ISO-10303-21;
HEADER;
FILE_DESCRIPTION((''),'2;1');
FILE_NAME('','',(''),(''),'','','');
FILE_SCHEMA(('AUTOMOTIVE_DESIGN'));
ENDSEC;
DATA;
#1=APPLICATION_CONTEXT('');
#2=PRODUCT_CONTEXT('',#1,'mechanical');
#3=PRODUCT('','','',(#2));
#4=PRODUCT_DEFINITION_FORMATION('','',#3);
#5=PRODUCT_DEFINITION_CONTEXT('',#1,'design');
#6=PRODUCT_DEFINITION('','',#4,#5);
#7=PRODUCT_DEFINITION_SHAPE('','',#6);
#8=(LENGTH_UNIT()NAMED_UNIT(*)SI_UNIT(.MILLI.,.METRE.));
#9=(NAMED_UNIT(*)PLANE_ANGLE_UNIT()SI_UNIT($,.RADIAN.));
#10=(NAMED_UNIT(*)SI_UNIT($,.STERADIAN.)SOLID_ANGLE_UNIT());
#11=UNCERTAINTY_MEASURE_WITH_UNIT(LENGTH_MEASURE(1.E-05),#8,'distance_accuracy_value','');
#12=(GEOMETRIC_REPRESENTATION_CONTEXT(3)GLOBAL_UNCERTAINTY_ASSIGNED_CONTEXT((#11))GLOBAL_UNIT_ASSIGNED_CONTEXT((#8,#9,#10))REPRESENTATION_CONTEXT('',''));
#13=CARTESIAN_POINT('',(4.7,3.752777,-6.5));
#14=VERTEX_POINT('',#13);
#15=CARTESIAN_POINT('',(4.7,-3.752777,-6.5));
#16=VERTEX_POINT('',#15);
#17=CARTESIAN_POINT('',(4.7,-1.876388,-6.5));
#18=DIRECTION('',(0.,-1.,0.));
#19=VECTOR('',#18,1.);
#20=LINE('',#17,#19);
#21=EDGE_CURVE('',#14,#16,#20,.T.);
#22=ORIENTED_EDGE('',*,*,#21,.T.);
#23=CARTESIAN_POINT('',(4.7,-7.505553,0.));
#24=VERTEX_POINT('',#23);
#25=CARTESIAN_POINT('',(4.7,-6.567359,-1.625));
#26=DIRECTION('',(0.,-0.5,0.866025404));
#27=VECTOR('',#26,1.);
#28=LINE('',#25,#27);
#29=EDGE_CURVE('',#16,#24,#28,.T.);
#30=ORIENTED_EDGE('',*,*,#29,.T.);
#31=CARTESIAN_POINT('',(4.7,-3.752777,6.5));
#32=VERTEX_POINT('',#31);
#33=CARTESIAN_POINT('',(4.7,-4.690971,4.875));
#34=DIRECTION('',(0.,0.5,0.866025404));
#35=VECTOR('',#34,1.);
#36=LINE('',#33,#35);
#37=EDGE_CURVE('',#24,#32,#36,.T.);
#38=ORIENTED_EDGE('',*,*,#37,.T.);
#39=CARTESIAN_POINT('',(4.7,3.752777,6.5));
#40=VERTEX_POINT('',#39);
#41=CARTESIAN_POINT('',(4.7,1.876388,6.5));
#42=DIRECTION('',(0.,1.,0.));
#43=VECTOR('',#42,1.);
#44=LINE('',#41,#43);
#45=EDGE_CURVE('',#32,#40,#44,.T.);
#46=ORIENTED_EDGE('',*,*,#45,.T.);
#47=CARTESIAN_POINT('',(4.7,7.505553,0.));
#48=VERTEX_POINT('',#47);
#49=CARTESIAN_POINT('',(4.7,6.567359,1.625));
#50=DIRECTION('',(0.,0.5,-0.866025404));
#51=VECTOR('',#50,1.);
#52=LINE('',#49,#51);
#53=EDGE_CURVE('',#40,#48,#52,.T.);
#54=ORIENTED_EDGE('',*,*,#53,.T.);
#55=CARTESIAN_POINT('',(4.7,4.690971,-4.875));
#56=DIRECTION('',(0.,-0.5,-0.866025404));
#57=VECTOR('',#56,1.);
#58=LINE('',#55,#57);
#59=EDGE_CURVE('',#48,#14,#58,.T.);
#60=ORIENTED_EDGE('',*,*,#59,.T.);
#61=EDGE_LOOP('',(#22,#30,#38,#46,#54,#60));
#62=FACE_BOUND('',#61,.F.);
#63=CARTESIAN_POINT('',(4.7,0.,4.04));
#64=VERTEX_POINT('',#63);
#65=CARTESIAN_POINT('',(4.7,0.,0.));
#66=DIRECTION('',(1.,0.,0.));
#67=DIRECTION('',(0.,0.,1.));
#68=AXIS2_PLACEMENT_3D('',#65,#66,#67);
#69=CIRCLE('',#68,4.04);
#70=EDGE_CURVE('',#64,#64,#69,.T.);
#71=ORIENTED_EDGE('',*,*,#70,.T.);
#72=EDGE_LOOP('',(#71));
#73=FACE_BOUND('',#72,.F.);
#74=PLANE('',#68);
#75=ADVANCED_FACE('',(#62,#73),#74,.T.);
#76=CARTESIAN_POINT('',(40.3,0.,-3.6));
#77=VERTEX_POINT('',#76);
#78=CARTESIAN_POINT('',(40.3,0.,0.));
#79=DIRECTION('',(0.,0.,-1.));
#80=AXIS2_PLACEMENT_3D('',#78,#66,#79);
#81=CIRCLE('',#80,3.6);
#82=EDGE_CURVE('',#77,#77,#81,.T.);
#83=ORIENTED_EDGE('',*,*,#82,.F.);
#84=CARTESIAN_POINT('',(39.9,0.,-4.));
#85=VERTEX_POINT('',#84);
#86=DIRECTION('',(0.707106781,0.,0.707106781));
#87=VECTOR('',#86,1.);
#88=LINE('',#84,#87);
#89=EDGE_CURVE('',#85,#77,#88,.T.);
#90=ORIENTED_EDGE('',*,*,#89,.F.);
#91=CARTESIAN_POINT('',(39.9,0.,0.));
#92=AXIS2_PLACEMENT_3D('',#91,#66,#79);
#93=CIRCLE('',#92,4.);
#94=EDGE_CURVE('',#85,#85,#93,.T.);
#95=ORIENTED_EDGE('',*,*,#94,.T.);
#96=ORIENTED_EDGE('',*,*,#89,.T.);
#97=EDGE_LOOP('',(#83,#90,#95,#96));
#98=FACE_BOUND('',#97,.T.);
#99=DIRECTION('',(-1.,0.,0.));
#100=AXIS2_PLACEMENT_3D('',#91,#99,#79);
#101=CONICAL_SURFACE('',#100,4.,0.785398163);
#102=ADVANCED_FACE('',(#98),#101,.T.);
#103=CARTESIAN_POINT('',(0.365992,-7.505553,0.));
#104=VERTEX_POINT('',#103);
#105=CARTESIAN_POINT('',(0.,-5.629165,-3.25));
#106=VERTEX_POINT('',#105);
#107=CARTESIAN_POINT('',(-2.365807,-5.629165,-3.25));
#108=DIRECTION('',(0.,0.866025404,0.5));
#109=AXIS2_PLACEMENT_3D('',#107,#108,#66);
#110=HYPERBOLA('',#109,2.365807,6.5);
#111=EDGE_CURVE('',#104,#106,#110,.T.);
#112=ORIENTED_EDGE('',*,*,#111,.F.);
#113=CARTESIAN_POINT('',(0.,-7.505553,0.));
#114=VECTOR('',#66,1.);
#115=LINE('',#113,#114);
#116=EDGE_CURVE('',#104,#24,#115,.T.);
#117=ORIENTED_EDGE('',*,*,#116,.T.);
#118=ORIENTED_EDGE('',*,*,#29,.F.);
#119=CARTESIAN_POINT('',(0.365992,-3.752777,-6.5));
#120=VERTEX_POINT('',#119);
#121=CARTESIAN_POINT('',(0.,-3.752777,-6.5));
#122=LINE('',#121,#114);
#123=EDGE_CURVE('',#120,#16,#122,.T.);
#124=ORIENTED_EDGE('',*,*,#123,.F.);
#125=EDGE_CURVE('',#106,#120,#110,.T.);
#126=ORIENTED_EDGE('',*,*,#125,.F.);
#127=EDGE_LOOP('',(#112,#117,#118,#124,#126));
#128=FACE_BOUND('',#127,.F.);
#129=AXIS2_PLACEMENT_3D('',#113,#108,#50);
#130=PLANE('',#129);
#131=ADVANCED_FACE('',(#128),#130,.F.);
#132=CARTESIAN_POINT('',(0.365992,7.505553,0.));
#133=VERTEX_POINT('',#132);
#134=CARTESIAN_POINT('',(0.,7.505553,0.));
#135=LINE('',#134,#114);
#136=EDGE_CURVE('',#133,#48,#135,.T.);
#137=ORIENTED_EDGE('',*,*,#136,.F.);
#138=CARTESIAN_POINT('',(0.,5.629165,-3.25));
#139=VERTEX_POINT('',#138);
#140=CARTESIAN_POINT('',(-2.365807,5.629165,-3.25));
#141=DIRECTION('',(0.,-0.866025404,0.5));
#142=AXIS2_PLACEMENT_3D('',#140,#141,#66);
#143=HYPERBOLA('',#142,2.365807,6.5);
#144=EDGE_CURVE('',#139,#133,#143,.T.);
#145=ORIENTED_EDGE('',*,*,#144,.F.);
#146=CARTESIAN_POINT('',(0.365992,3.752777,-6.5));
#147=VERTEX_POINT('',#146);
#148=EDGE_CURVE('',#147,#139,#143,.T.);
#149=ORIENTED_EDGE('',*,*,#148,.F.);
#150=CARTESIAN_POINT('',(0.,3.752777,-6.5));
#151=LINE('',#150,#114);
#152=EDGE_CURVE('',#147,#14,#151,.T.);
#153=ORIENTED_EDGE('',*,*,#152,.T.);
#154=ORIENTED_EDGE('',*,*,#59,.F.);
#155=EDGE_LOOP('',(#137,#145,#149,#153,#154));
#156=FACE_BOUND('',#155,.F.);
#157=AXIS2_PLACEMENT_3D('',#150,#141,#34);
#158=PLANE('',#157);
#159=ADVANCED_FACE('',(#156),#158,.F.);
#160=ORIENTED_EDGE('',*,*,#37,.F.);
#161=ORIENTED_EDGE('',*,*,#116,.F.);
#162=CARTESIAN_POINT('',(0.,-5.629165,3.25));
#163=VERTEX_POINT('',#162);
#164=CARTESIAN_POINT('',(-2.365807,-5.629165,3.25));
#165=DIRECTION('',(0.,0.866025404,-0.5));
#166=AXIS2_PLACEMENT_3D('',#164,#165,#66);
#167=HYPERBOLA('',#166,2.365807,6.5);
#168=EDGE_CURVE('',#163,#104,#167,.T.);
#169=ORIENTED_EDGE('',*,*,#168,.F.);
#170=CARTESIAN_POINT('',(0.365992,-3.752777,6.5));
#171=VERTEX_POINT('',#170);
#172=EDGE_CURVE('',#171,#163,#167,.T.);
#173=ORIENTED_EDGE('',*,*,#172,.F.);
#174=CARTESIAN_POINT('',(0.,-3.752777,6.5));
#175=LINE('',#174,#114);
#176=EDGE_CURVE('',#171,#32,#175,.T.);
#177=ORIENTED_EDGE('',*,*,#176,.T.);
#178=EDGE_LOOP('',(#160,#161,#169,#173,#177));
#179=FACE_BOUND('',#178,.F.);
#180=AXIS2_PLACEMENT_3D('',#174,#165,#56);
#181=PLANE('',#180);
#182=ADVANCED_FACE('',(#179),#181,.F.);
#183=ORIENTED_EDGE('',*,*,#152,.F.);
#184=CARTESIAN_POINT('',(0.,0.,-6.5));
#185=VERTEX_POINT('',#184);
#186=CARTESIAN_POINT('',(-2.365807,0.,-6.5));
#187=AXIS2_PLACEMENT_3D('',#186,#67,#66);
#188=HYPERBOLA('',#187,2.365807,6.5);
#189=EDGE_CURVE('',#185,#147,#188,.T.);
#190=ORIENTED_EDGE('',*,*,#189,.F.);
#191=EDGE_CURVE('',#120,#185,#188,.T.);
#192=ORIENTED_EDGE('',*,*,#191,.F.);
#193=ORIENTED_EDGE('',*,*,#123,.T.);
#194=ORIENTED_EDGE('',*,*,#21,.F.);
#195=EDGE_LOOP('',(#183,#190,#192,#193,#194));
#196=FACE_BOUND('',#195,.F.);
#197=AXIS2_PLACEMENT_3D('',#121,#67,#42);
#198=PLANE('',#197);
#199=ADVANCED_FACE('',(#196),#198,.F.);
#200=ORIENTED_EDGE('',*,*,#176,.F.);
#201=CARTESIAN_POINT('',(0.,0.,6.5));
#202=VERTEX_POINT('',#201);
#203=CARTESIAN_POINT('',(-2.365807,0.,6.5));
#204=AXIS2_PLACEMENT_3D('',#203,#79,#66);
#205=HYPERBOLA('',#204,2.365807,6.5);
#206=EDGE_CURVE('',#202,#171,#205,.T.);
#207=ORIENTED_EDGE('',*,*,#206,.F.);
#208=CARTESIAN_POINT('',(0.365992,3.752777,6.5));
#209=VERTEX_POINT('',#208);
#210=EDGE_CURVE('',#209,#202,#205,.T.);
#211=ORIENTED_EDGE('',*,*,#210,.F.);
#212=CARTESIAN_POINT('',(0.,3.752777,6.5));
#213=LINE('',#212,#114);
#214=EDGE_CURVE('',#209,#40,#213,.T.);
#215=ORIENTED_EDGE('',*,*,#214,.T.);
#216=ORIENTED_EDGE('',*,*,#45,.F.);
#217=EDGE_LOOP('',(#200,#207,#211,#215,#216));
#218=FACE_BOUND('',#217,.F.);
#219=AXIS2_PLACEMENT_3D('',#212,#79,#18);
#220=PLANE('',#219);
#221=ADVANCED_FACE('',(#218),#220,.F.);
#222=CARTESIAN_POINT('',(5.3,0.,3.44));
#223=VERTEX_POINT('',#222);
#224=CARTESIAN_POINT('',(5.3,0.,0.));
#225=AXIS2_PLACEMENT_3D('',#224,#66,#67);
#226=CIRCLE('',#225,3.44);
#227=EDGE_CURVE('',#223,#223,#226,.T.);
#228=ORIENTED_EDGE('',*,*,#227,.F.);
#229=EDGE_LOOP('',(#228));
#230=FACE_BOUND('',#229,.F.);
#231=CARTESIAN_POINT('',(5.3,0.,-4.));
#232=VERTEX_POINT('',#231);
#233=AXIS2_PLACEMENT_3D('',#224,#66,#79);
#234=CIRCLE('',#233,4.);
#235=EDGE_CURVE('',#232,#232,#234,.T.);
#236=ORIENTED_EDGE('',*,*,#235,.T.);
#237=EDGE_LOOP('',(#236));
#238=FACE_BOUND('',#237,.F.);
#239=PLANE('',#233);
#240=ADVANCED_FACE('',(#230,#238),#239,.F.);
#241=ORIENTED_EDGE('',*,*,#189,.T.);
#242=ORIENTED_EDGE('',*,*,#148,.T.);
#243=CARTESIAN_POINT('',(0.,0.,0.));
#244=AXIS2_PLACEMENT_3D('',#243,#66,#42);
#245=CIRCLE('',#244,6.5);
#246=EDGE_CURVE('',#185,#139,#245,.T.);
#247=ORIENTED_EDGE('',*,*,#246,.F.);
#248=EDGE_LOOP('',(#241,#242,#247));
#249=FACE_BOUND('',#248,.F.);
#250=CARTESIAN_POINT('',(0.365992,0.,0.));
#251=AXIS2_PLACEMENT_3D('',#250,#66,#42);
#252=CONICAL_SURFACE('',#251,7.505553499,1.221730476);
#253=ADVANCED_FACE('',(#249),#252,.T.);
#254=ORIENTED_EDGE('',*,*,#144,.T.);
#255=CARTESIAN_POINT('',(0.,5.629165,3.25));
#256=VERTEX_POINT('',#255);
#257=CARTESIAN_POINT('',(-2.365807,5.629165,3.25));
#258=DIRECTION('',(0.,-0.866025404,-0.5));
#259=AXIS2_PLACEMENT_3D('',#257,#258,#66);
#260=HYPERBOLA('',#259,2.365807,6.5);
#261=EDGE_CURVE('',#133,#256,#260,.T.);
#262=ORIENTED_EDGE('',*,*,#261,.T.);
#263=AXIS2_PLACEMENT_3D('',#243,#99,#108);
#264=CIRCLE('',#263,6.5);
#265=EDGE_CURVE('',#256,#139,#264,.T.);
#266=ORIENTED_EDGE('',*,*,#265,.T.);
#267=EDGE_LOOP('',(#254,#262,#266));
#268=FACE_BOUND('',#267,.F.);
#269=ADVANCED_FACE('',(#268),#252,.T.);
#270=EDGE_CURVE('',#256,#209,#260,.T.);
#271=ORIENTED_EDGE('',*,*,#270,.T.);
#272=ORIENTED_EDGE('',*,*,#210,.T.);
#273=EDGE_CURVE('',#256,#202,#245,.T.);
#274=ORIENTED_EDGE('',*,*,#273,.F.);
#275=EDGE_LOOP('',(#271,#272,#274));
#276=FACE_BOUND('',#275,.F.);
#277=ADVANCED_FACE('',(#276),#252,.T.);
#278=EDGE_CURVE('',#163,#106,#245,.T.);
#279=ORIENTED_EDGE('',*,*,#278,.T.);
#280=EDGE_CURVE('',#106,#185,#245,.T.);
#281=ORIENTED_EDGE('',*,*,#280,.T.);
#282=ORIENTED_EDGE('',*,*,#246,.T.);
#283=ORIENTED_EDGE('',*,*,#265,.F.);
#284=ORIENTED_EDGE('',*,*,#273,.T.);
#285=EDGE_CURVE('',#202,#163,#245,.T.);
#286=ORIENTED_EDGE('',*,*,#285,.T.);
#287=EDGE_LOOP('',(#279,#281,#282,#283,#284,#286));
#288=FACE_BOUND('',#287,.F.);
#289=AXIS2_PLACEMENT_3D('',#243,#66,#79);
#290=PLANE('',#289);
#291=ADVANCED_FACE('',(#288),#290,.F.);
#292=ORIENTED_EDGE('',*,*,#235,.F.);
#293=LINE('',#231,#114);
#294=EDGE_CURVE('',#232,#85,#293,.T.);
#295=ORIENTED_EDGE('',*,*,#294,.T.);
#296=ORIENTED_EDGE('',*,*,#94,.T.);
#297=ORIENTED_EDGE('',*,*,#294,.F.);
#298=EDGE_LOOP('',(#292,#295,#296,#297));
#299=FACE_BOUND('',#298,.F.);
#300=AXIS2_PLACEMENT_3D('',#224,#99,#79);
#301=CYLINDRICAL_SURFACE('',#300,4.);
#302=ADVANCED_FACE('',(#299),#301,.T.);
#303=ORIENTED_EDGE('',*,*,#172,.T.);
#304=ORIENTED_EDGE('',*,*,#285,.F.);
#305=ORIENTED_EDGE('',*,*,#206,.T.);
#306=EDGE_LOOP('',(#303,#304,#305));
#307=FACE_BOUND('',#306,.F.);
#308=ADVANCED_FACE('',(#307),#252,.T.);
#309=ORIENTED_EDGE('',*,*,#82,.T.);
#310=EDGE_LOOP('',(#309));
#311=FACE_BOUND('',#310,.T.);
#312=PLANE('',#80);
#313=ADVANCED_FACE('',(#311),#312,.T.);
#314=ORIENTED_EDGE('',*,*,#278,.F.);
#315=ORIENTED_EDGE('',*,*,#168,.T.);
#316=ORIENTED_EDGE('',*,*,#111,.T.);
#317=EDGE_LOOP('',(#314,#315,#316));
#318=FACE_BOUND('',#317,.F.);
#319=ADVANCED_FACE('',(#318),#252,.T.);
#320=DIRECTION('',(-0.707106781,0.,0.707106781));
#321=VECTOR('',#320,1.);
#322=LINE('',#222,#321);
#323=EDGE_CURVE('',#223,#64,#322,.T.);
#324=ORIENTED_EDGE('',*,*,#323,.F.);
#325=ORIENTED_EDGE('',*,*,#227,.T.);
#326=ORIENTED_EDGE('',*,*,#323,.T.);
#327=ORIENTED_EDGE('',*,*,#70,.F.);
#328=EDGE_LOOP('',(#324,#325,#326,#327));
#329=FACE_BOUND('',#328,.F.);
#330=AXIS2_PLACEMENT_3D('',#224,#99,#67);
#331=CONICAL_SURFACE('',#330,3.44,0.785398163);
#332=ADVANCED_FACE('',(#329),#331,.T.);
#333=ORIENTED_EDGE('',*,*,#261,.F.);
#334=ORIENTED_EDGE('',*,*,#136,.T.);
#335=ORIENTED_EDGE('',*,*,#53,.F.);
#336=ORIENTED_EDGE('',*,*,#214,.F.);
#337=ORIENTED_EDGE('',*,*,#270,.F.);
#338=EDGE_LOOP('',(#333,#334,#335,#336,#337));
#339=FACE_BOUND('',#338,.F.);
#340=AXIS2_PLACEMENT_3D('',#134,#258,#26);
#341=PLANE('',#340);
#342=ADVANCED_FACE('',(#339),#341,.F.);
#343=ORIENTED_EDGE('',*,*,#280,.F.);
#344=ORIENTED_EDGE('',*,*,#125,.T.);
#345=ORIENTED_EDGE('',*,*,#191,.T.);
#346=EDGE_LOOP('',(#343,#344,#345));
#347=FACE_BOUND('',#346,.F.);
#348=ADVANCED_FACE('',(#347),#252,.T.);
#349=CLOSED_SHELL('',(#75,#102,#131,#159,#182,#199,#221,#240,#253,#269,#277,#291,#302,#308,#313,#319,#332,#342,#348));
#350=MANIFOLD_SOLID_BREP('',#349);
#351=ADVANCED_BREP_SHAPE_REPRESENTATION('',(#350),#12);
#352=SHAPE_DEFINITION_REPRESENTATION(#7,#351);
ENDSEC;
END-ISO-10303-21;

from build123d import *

# Parameters (mm, degrees)
BASEHEAD_DEPTH = 5.3
SKETCH5_R      = 4
BASEBODY_DEPTH = 35
CHAMFER1_SIZE  = 0.4


with BuildPart() as part:
    # Sketch2 → BaseHead (new body)
    with BuildSketch(Plane(origin=(0, 0, 0), x_dir=(0, 0, -1), z_dir=(1, 0, 0))):
        Polygon((6.5, -3.75277675), (6.5, 3.75277675), (0, 7.505553499), (-6.5, 3.75277675), (-6.5, -3.75277675), (0, -7.505553499), align=None)
    extrude(amount=BASEHEAD_DEPTH)

    # Sketch3 → BearingFace (revolve, cut)
    with BuildSketch(Plane.XY, mode=Mode.PRIVATE) as bearingface_sk:
        Polygon((5.3, 7.505553499), (5.3, 3.44), (4.7, 4.04), (4.7, 7.505553499), align=None)
    revolve(bearingface_sk.sketch.rotate(Axis((-0.957090588, 0, 0), (1, 0, 0)), 90), axis=Axis((-0.957090588, 0, 0), (1, 0, 0)), mode=Mode.SUBTRACT)

    # Sketch4 → HeadChamfer (revolve, cut)
    with BuildSketch(Plane.XY):
        Polygon((0, 7.505553499), (0.365991543, 7.505553499), (0, 6.5), align=None)
    revolve(axis=Axis((-0.493528746, 0, 0), (1, 0, 0)), mode=Mode.SUBTRACT)

    # Sketch5 → BaseBody (add)
    with BuildSketch(Plane(origin=(5.3, 0, 0), x_dir=(0, 0, -1), z_dir=(1, 0, 0))):
        Circle(SKETCH5_R)
    extrude(amount=BASEBODY_DEPTH)

    # Chamfer1
    chamfer1_edges = [part.edges().sort_by_distance(p)[0] for p in [
        (40.3, 0, 4),
    ]]
    chamfer(chamfer1_edges, length=CHAMFER1_SIZE)


solid = part.part
